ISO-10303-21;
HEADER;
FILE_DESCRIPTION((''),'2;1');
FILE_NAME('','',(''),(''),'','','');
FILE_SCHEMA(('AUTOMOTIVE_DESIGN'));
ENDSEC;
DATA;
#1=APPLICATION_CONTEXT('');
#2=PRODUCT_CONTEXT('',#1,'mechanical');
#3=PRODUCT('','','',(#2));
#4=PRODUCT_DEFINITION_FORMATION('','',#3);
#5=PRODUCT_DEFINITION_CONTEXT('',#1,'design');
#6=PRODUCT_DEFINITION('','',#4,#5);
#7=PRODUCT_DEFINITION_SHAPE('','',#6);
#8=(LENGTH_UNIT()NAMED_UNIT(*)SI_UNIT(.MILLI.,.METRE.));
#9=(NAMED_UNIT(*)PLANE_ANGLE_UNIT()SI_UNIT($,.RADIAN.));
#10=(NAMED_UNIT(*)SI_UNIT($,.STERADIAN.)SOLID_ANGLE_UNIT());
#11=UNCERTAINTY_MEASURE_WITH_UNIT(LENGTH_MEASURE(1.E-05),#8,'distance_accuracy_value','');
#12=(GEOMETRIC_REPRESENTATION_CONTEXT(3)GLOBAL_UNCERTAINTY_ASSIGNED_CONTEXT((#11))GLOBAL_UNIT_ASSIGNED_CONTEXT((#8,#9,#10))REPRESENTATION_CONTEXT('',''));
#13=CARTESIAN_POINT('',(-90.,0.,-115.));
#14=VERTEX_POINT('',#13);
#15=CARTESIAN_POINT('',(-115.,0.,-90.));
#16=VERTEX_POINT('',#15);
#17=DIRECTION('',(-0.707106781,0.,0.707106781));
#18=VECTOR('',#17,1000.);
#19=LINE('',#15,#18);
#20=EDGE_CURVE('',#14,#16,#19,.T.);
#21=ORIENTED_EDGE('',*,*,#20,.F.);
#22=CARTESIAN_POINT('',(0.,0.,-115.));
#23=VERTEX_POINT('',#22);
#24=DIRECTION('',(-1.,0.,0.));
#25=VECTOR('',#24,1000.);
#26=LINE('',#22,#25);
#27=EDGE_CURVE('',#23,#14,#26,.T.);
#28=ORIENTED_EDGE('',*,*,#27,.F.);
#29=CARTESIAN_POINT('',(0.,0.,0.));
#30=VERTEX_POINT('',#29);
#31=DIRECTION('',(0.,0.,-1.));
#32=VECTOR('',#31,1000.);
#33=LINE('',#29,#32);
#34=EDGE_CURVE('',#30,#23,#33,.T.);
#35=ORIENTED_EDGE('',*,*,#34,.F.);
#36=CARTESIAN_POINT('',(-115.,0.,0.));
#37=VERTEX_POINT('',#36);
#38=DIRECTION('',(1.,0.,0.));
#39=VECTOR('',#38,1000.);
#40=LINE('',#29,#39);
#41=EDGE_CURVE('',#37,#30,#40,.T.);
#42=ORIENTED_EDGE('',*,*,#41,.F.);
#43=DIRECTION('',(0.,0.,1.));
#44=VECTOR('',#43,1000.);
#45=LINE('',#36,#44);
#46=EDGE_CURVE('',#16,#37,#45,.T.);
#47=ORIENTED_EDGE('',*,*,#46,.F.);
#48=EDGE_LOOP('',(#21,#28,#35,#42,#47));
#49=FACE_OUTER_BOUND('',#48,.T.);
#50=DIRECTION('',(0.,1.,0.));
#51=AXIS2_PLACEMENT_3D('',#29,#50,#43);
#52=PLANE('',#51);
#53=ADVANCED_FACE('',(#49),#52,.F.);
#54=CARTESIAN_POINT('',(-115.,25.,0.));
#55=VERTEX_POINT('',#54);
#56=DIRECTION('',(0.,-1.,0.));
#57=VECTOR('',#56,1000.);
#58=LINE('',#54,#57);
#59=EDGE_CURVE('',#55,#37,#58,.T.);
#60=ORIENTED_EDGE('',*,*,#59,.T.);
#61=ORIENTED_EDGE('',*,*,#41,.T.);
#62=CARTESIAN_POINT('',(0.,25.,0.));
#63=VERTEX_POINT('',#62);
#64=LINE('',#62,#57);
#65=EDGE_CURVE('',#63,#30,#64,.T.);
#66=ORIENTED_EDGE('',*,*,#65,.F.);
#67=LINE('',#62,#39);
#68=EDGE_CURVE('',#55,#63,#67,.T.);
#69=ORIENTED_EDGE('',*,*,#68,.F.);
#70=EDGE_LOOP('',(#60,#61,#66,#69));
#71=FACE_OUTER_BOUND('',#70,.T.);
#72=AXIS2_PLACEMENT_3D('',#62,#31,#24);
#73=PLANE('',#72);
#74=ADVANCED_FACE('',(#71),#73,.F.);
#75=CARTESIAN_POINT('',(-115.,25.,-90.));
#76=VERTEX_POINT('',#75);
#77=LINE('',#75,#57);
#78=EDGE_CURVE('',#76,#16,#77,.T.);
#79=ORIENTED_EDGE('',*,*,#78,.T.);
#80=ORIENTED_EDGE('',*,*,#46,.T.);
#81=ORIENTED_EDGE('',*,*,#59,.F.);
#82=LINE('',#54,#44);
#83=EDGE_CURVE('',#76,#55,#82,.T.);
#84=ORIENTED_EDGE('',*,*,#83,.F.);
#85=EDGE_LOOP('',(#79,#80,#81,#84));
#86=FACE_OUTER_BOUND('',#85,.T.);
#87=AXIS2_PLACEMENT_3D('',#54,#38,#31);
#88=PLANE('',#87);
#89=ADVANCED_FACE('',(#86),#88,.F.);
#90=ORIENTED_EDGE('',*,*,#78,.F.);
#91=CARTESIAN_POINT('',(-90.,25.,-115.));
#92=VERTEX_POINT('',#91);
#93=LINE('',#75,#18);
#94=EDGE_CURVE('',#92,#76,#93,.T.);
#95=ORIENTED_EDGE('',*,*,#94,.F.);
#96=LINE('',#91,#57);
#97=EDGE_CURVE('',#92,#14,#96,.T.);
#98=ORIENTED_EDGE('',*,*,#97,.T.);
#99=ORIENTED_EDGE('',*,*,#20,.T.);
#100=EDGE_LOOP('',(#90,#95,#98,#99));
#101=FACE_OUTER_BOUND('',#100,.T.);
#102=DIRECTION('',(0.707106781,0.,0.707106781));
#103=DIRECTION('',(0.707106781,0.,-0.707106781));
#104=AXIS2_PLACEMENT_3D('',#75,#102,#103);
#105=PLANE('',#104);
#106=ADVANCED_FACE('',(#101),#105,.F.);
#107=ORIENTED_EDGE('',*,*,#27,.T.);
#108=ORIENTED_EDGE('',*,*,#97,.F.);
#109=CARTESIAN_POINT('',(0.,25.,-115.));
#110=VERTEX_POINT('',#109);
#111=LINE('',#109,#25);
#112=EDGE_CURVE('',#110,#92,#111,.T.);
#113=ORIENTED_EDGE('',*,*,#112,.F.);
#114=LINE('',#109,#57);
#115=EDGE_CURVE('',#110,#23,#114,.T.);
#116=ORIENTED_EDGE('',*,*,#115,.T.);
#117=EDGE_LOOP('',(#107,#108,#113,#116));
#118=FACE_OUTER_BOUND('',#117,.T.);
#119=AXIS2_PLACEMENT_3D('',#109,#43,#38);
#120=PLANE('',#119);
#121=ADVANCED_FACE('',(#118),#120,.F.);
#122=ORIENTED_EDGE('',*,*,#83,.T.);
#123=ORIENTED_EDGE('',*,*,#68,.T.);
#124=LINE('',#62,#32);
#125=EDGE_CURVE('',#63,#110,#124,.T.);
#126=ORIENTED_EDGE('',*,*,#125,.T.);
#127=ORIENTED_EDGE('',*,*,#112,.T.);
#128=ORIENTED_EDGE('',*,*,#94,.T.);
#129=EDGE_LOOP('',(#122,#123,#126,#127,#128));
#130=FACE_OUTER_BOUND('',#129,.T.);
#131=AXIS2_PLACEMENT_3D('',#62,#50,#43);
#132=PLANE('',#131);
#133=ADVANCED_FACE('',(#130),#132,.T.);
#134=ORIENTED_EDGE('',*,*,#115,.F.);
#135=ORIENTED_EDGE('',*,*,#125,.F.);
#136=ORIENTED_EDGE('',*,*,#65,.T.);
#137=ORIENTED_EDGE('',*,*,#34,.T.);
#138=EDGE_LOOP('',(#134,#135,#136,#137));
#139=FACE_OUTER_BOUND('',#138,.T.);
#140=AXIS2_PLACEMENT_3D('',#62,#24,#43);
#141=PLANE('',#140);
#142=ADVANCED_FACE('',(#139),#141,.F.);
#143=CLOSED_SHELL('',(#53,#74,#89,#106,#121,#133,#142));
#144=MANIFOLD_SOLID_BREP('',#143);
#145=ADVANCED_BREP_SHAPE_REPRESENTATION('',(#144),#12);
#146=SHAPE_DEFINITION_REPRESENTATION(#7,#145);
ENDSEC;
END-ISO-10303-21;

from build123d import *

# Parameters (mm, degrees)
EXTRUDE_1_DEPTH = 25


with BuildPart() as part:
    # 草图1 → 凸台-拉伸1 (new body)
    with BuildSketch(Plane(origin=(0, 0, 0), x_dir=(1, 0, 0), z_dir=(0, 1, 0))):
        Polygon((-115, 90), (-90, 115), (0, 115), (0, 0), (-115, 0), align=None)
    extrude(amount=EXTRUDE_1_DEPTH)


solid = part.part
